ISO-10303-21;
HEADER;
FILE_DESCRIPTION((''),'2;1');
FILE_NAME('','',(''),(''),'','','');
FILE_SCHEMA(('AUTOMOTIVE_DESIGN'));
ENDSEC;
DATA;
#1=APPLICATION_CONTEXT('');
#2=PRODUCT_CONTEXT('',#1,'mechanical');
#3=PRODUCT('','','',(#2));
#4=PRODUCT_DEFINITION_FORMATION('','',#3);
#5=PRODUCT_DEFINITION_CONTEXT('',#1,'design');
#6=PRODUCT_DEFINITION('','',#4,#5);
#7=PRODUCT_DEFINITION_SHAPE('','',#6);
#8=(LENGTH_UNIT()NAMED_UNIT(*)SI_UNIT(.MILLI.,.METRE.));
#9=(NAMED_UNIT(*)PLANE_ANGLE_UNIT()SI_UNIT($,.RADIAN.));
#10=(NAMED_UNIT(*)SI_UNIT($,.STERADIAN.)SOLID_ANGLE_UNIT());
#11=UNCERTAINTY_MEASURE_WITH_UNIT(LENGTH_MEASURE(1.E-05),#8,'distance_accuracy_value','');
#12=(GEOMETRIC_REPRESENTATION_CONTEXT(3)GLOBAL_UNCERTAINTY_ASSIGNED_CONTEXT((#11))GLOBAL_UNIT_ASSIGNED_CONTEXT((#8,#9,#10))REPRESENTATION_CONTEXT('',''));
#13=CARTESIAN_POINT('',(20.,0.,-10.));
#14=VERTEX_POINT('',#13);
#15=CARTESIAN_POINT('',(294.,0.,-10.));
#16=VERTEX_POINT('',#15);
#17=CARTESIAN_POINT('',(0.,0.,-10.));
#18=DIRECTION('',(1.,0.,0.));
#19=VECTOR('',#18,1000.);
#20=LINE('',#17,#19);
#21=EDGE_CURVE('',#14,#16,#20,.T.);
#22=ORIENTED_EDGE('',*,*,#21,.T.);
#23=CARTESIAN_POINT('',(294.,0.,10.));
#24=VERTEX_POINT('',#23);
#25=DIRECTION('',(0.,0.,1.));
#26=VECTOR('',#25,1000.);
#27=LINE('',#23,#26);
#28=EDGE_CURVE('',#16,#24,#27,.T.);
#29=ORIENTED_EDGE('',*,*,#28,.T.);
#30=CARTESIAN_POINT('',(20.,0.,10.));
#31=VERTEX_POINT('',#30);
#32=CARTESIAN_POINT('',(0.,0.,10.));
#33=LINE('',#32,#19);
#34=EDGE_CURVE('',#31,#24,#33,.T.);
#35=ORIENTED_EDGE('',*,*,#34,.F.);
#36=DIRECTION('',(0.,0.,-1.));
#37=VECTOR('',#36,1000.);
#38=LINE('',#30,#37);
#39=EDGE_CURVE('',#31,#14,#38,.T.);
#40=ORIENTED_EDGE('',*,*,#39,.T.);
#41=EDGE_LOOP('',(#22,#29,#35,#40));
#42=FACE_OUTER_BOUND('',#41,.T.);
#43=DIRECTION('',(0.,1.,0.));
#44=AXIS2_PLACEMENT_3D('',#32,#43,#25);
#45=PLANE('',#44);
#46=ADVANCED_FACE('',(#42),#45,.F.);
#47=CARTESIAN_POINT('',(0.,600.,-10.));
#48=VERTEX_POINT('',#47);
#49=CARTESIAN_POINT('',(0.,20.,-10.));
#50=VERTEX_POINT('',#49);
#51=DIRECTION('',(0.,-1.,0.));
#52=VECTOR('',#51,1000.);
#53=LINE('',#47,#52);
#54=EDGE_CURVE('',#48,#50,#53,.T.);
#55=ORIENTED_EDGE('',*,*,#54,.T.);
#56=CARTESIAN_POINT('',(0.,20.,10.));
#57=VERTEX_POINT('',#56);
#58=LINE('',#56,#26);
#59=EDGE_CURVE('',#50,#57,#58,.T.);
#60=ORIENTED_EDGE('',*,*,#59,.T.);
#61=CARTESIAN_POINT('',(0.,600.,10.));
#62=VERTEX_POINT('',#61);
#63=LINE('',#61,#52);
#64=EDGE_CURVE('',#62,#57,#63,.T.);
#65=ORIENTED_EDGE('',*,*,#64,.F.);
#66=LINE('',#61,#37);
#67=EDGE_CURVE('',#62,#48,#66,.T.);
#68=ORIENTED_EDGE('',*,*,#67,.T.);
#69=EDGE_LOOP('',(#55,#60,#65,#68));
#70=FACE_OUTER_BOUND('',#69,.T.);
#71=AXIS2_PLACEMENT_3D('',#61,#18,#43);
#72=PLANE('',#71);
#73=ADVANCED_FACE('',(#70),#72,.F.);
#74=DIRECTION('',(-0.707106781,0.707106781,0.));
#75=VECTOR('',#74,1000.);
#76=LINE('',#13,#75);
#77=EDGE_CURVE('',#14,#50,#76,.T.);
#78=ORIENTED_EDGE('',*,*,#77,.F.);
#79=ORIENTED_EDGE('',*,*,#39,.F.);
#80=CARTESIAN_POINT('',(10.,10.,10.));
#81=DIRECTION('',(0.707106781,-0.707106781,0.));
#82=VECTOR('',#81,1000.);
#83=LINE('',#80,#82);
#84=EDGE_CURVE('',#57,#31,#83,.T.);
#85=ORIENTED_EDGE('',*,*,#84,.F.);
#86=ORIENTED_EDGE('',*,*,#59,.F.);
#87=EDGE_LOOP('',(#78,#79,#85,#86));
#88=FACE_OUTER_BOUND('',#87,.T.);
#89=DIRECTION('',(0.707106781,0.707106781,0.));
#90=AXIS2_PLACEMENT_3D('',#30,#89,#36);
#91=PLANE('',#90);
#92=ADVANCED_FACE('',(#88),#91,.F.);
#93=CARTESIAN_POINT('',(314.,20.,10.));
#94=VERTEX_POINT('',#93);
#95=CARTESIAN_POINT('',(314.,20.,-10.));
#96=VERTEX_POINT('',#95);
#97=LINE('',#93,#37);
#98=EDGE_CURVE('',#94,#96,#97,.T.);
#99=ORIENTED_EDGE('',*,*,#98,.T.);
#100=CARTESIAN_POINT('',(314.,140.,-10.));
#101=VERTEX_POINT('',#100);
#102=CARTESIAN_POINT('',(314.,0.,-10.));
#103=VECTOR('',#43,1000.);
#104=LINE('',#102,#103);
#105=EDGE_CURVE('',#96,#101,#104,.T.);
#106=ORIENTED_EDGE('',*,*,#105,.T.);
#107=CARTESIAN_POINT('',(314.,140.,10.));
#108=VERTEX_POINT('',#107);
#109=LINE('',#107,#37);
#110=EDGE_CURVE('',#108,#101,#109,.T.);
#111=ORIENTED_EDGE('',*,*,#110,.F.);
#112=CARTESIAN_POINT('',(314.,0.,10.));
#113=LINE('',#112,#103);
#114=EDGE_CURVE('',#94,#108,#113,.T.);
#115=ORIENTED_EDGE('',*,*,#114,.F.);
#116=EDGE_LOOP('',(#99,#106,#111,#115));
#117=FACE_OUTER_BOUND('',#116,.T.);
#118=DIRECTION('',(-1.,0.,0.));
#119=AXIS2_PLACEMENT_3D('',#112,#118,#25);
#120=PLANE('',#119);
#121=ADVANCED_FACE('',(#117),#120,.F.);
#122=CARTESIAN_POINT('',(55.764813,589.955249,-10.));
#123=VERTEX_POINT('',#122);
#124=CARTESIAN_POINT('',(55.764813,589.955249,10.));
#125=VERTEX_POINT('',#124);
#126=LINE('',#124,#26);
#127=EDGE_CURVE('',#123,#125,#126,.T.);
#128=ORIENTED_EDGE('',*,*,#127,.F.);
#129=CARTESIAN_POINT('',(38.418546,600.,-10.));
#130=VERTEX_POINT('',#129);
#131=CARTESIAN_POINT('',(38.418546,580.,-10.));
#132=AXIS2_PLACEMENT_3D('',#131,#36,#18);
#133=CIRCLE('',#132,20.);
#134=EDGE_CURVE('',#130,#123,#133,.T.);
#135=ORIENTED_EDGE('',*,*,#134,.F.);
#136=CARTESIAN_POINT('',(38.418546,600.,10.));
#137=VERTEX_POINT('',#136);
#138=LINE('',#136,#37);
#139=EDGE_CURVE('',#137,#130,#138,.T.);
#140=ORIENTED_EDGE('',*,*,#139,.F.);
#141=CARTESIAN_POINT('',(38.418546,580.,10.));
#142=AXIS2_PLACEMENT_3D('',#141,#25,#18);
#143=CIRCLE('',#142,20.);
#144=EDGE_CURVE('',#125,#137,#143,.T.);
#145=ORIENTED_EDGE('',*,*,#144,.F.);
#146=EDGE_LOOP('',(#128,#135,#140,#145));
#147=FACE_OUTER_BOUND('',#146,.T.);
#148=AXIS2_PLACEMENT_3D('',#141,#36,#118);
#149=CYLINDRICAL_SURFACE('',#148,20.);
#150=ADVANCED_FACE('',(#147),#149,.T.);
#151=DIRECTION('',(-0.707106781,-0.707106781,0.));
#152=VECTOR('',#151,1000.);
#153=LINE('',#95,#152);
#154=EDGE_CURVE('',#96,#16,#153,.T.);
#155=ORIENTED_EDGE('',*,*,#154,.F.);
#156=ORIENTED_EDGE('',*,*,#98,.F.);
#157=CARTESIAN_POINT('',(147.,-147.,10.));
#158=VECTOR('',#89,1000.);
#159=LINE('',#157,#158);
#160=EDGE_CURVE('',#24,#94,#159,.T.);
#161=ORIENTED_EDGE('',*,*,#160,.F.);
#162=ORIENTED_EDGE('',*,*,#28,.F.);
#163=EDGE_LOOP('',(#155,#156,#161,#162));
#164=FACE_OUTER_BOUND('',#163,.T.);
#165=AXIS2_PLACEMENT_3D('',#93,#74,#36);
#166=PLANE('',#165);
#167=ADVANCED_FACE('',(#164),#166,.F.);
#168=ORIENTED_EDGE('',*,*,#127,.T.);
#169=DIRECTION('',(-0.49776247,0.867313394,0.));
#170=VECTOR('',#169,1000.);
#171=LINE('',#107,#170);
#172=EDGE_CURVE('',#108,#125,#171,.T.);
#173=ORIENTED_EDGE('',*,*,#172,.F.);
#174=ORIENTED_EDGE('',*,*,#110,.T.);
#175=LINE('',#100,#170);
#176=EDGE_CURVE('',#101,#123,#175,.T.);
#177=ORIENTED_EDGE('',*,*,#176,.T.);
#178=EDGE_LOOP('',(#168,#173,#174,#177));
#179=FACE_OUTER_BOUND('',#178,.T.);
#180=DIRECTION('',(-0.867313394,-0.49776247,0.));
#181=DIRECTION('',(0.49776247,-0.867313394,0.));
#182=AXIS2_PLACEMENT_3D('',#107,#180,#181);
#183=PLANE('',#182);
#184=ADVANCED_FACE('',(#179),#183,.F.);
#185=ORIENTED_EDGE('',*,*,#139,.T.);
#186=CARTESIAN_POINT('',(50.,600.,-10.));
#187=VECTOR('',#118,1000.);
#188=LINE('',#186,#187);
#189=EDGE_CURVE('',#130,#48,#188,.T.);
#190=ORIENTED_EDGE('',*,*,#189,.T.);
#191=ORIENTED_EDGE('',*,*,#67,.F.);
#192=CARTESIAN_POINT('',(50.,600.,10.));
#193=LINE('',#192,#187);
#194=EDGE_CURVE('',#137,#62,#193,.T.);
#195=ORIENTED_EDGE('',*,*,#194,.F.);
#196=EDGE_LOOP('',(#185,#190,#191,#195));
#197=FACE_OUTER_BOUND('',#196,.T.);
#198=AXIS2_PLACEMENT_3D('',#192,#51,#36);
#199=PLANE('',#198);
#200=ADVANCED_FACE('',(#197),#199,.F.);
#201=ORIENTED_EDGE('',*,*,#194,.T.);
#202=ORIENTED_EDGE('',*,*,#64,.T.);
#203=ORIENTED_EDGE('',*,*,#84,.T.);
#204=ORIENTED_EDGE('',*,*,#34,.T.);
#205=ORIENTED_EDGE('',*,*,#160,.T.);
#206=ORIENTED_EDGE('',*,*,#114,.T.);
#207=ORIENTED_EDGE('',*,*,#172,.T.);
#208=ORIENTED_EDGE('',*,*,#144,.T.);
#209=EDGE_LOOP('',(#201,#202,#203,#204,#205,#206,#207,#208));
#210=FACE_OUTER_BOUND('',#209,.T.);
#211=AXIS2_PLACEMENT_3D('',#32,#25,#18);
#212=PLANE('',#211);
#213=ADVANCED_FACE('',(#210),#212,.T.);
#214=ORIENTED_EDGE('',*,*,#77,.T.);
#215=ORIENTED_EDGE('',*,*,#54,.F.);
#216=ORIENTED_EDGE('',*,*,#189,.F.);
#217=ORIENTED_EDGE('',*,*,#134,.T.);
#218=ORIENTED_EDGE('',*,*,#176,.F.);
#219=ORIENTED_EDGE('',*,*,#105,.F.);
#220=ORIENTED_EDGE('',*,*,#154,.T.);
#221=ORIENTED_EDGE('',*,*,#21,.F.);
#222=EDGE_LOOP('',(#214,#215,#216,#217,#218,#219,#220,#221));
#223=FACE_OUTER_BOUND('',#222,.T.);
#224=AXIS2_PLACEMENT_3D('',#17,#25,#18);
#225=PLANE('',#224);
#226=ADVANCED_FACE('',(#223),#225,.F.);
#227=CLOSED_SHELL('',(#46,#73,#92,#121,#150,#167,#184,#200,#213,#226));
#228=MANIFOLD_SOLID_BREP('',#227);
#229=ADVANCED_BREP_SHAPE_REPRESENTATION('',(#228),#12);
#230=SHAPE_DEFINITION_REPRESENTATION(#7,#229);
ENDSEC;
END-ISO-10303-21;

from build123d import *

# Parameters (mm, degrees)
BOSS_EXTRUDE1_DEPTH = 10
FILLET1_R           = 20
CHAMFER1_SIZE       = 20


with BuildPart() as part:
    # Sketch1 → Boss-Extrude1 (new, symmetric)
    with BuildSketch(Plane.XY):
        Polygon((0, 0), (314, 0), (314, 140), (50, 600), (0, 600), align=None)
    extrude(amount=BOSS_EXTRUDE1_DEPTH, both=True)

    # Fillet1
    fillet1_edges = [part.edges().sort_by_distance(p)[0] for p in [
        (50, 600, 0),
    ]]
    fillet(fillet1_edges, radius=FILLET1_R)

    # Chamfer1
    chamfer1_edges = [part.edges().sort_by_distance(p)[0] for p in [
        (314, 0, 0),
        (0, 0, 0),
    ]]
    chamfer(chamfer1_edges, length=CHAMFER1_SIZE)


solid = part.part
